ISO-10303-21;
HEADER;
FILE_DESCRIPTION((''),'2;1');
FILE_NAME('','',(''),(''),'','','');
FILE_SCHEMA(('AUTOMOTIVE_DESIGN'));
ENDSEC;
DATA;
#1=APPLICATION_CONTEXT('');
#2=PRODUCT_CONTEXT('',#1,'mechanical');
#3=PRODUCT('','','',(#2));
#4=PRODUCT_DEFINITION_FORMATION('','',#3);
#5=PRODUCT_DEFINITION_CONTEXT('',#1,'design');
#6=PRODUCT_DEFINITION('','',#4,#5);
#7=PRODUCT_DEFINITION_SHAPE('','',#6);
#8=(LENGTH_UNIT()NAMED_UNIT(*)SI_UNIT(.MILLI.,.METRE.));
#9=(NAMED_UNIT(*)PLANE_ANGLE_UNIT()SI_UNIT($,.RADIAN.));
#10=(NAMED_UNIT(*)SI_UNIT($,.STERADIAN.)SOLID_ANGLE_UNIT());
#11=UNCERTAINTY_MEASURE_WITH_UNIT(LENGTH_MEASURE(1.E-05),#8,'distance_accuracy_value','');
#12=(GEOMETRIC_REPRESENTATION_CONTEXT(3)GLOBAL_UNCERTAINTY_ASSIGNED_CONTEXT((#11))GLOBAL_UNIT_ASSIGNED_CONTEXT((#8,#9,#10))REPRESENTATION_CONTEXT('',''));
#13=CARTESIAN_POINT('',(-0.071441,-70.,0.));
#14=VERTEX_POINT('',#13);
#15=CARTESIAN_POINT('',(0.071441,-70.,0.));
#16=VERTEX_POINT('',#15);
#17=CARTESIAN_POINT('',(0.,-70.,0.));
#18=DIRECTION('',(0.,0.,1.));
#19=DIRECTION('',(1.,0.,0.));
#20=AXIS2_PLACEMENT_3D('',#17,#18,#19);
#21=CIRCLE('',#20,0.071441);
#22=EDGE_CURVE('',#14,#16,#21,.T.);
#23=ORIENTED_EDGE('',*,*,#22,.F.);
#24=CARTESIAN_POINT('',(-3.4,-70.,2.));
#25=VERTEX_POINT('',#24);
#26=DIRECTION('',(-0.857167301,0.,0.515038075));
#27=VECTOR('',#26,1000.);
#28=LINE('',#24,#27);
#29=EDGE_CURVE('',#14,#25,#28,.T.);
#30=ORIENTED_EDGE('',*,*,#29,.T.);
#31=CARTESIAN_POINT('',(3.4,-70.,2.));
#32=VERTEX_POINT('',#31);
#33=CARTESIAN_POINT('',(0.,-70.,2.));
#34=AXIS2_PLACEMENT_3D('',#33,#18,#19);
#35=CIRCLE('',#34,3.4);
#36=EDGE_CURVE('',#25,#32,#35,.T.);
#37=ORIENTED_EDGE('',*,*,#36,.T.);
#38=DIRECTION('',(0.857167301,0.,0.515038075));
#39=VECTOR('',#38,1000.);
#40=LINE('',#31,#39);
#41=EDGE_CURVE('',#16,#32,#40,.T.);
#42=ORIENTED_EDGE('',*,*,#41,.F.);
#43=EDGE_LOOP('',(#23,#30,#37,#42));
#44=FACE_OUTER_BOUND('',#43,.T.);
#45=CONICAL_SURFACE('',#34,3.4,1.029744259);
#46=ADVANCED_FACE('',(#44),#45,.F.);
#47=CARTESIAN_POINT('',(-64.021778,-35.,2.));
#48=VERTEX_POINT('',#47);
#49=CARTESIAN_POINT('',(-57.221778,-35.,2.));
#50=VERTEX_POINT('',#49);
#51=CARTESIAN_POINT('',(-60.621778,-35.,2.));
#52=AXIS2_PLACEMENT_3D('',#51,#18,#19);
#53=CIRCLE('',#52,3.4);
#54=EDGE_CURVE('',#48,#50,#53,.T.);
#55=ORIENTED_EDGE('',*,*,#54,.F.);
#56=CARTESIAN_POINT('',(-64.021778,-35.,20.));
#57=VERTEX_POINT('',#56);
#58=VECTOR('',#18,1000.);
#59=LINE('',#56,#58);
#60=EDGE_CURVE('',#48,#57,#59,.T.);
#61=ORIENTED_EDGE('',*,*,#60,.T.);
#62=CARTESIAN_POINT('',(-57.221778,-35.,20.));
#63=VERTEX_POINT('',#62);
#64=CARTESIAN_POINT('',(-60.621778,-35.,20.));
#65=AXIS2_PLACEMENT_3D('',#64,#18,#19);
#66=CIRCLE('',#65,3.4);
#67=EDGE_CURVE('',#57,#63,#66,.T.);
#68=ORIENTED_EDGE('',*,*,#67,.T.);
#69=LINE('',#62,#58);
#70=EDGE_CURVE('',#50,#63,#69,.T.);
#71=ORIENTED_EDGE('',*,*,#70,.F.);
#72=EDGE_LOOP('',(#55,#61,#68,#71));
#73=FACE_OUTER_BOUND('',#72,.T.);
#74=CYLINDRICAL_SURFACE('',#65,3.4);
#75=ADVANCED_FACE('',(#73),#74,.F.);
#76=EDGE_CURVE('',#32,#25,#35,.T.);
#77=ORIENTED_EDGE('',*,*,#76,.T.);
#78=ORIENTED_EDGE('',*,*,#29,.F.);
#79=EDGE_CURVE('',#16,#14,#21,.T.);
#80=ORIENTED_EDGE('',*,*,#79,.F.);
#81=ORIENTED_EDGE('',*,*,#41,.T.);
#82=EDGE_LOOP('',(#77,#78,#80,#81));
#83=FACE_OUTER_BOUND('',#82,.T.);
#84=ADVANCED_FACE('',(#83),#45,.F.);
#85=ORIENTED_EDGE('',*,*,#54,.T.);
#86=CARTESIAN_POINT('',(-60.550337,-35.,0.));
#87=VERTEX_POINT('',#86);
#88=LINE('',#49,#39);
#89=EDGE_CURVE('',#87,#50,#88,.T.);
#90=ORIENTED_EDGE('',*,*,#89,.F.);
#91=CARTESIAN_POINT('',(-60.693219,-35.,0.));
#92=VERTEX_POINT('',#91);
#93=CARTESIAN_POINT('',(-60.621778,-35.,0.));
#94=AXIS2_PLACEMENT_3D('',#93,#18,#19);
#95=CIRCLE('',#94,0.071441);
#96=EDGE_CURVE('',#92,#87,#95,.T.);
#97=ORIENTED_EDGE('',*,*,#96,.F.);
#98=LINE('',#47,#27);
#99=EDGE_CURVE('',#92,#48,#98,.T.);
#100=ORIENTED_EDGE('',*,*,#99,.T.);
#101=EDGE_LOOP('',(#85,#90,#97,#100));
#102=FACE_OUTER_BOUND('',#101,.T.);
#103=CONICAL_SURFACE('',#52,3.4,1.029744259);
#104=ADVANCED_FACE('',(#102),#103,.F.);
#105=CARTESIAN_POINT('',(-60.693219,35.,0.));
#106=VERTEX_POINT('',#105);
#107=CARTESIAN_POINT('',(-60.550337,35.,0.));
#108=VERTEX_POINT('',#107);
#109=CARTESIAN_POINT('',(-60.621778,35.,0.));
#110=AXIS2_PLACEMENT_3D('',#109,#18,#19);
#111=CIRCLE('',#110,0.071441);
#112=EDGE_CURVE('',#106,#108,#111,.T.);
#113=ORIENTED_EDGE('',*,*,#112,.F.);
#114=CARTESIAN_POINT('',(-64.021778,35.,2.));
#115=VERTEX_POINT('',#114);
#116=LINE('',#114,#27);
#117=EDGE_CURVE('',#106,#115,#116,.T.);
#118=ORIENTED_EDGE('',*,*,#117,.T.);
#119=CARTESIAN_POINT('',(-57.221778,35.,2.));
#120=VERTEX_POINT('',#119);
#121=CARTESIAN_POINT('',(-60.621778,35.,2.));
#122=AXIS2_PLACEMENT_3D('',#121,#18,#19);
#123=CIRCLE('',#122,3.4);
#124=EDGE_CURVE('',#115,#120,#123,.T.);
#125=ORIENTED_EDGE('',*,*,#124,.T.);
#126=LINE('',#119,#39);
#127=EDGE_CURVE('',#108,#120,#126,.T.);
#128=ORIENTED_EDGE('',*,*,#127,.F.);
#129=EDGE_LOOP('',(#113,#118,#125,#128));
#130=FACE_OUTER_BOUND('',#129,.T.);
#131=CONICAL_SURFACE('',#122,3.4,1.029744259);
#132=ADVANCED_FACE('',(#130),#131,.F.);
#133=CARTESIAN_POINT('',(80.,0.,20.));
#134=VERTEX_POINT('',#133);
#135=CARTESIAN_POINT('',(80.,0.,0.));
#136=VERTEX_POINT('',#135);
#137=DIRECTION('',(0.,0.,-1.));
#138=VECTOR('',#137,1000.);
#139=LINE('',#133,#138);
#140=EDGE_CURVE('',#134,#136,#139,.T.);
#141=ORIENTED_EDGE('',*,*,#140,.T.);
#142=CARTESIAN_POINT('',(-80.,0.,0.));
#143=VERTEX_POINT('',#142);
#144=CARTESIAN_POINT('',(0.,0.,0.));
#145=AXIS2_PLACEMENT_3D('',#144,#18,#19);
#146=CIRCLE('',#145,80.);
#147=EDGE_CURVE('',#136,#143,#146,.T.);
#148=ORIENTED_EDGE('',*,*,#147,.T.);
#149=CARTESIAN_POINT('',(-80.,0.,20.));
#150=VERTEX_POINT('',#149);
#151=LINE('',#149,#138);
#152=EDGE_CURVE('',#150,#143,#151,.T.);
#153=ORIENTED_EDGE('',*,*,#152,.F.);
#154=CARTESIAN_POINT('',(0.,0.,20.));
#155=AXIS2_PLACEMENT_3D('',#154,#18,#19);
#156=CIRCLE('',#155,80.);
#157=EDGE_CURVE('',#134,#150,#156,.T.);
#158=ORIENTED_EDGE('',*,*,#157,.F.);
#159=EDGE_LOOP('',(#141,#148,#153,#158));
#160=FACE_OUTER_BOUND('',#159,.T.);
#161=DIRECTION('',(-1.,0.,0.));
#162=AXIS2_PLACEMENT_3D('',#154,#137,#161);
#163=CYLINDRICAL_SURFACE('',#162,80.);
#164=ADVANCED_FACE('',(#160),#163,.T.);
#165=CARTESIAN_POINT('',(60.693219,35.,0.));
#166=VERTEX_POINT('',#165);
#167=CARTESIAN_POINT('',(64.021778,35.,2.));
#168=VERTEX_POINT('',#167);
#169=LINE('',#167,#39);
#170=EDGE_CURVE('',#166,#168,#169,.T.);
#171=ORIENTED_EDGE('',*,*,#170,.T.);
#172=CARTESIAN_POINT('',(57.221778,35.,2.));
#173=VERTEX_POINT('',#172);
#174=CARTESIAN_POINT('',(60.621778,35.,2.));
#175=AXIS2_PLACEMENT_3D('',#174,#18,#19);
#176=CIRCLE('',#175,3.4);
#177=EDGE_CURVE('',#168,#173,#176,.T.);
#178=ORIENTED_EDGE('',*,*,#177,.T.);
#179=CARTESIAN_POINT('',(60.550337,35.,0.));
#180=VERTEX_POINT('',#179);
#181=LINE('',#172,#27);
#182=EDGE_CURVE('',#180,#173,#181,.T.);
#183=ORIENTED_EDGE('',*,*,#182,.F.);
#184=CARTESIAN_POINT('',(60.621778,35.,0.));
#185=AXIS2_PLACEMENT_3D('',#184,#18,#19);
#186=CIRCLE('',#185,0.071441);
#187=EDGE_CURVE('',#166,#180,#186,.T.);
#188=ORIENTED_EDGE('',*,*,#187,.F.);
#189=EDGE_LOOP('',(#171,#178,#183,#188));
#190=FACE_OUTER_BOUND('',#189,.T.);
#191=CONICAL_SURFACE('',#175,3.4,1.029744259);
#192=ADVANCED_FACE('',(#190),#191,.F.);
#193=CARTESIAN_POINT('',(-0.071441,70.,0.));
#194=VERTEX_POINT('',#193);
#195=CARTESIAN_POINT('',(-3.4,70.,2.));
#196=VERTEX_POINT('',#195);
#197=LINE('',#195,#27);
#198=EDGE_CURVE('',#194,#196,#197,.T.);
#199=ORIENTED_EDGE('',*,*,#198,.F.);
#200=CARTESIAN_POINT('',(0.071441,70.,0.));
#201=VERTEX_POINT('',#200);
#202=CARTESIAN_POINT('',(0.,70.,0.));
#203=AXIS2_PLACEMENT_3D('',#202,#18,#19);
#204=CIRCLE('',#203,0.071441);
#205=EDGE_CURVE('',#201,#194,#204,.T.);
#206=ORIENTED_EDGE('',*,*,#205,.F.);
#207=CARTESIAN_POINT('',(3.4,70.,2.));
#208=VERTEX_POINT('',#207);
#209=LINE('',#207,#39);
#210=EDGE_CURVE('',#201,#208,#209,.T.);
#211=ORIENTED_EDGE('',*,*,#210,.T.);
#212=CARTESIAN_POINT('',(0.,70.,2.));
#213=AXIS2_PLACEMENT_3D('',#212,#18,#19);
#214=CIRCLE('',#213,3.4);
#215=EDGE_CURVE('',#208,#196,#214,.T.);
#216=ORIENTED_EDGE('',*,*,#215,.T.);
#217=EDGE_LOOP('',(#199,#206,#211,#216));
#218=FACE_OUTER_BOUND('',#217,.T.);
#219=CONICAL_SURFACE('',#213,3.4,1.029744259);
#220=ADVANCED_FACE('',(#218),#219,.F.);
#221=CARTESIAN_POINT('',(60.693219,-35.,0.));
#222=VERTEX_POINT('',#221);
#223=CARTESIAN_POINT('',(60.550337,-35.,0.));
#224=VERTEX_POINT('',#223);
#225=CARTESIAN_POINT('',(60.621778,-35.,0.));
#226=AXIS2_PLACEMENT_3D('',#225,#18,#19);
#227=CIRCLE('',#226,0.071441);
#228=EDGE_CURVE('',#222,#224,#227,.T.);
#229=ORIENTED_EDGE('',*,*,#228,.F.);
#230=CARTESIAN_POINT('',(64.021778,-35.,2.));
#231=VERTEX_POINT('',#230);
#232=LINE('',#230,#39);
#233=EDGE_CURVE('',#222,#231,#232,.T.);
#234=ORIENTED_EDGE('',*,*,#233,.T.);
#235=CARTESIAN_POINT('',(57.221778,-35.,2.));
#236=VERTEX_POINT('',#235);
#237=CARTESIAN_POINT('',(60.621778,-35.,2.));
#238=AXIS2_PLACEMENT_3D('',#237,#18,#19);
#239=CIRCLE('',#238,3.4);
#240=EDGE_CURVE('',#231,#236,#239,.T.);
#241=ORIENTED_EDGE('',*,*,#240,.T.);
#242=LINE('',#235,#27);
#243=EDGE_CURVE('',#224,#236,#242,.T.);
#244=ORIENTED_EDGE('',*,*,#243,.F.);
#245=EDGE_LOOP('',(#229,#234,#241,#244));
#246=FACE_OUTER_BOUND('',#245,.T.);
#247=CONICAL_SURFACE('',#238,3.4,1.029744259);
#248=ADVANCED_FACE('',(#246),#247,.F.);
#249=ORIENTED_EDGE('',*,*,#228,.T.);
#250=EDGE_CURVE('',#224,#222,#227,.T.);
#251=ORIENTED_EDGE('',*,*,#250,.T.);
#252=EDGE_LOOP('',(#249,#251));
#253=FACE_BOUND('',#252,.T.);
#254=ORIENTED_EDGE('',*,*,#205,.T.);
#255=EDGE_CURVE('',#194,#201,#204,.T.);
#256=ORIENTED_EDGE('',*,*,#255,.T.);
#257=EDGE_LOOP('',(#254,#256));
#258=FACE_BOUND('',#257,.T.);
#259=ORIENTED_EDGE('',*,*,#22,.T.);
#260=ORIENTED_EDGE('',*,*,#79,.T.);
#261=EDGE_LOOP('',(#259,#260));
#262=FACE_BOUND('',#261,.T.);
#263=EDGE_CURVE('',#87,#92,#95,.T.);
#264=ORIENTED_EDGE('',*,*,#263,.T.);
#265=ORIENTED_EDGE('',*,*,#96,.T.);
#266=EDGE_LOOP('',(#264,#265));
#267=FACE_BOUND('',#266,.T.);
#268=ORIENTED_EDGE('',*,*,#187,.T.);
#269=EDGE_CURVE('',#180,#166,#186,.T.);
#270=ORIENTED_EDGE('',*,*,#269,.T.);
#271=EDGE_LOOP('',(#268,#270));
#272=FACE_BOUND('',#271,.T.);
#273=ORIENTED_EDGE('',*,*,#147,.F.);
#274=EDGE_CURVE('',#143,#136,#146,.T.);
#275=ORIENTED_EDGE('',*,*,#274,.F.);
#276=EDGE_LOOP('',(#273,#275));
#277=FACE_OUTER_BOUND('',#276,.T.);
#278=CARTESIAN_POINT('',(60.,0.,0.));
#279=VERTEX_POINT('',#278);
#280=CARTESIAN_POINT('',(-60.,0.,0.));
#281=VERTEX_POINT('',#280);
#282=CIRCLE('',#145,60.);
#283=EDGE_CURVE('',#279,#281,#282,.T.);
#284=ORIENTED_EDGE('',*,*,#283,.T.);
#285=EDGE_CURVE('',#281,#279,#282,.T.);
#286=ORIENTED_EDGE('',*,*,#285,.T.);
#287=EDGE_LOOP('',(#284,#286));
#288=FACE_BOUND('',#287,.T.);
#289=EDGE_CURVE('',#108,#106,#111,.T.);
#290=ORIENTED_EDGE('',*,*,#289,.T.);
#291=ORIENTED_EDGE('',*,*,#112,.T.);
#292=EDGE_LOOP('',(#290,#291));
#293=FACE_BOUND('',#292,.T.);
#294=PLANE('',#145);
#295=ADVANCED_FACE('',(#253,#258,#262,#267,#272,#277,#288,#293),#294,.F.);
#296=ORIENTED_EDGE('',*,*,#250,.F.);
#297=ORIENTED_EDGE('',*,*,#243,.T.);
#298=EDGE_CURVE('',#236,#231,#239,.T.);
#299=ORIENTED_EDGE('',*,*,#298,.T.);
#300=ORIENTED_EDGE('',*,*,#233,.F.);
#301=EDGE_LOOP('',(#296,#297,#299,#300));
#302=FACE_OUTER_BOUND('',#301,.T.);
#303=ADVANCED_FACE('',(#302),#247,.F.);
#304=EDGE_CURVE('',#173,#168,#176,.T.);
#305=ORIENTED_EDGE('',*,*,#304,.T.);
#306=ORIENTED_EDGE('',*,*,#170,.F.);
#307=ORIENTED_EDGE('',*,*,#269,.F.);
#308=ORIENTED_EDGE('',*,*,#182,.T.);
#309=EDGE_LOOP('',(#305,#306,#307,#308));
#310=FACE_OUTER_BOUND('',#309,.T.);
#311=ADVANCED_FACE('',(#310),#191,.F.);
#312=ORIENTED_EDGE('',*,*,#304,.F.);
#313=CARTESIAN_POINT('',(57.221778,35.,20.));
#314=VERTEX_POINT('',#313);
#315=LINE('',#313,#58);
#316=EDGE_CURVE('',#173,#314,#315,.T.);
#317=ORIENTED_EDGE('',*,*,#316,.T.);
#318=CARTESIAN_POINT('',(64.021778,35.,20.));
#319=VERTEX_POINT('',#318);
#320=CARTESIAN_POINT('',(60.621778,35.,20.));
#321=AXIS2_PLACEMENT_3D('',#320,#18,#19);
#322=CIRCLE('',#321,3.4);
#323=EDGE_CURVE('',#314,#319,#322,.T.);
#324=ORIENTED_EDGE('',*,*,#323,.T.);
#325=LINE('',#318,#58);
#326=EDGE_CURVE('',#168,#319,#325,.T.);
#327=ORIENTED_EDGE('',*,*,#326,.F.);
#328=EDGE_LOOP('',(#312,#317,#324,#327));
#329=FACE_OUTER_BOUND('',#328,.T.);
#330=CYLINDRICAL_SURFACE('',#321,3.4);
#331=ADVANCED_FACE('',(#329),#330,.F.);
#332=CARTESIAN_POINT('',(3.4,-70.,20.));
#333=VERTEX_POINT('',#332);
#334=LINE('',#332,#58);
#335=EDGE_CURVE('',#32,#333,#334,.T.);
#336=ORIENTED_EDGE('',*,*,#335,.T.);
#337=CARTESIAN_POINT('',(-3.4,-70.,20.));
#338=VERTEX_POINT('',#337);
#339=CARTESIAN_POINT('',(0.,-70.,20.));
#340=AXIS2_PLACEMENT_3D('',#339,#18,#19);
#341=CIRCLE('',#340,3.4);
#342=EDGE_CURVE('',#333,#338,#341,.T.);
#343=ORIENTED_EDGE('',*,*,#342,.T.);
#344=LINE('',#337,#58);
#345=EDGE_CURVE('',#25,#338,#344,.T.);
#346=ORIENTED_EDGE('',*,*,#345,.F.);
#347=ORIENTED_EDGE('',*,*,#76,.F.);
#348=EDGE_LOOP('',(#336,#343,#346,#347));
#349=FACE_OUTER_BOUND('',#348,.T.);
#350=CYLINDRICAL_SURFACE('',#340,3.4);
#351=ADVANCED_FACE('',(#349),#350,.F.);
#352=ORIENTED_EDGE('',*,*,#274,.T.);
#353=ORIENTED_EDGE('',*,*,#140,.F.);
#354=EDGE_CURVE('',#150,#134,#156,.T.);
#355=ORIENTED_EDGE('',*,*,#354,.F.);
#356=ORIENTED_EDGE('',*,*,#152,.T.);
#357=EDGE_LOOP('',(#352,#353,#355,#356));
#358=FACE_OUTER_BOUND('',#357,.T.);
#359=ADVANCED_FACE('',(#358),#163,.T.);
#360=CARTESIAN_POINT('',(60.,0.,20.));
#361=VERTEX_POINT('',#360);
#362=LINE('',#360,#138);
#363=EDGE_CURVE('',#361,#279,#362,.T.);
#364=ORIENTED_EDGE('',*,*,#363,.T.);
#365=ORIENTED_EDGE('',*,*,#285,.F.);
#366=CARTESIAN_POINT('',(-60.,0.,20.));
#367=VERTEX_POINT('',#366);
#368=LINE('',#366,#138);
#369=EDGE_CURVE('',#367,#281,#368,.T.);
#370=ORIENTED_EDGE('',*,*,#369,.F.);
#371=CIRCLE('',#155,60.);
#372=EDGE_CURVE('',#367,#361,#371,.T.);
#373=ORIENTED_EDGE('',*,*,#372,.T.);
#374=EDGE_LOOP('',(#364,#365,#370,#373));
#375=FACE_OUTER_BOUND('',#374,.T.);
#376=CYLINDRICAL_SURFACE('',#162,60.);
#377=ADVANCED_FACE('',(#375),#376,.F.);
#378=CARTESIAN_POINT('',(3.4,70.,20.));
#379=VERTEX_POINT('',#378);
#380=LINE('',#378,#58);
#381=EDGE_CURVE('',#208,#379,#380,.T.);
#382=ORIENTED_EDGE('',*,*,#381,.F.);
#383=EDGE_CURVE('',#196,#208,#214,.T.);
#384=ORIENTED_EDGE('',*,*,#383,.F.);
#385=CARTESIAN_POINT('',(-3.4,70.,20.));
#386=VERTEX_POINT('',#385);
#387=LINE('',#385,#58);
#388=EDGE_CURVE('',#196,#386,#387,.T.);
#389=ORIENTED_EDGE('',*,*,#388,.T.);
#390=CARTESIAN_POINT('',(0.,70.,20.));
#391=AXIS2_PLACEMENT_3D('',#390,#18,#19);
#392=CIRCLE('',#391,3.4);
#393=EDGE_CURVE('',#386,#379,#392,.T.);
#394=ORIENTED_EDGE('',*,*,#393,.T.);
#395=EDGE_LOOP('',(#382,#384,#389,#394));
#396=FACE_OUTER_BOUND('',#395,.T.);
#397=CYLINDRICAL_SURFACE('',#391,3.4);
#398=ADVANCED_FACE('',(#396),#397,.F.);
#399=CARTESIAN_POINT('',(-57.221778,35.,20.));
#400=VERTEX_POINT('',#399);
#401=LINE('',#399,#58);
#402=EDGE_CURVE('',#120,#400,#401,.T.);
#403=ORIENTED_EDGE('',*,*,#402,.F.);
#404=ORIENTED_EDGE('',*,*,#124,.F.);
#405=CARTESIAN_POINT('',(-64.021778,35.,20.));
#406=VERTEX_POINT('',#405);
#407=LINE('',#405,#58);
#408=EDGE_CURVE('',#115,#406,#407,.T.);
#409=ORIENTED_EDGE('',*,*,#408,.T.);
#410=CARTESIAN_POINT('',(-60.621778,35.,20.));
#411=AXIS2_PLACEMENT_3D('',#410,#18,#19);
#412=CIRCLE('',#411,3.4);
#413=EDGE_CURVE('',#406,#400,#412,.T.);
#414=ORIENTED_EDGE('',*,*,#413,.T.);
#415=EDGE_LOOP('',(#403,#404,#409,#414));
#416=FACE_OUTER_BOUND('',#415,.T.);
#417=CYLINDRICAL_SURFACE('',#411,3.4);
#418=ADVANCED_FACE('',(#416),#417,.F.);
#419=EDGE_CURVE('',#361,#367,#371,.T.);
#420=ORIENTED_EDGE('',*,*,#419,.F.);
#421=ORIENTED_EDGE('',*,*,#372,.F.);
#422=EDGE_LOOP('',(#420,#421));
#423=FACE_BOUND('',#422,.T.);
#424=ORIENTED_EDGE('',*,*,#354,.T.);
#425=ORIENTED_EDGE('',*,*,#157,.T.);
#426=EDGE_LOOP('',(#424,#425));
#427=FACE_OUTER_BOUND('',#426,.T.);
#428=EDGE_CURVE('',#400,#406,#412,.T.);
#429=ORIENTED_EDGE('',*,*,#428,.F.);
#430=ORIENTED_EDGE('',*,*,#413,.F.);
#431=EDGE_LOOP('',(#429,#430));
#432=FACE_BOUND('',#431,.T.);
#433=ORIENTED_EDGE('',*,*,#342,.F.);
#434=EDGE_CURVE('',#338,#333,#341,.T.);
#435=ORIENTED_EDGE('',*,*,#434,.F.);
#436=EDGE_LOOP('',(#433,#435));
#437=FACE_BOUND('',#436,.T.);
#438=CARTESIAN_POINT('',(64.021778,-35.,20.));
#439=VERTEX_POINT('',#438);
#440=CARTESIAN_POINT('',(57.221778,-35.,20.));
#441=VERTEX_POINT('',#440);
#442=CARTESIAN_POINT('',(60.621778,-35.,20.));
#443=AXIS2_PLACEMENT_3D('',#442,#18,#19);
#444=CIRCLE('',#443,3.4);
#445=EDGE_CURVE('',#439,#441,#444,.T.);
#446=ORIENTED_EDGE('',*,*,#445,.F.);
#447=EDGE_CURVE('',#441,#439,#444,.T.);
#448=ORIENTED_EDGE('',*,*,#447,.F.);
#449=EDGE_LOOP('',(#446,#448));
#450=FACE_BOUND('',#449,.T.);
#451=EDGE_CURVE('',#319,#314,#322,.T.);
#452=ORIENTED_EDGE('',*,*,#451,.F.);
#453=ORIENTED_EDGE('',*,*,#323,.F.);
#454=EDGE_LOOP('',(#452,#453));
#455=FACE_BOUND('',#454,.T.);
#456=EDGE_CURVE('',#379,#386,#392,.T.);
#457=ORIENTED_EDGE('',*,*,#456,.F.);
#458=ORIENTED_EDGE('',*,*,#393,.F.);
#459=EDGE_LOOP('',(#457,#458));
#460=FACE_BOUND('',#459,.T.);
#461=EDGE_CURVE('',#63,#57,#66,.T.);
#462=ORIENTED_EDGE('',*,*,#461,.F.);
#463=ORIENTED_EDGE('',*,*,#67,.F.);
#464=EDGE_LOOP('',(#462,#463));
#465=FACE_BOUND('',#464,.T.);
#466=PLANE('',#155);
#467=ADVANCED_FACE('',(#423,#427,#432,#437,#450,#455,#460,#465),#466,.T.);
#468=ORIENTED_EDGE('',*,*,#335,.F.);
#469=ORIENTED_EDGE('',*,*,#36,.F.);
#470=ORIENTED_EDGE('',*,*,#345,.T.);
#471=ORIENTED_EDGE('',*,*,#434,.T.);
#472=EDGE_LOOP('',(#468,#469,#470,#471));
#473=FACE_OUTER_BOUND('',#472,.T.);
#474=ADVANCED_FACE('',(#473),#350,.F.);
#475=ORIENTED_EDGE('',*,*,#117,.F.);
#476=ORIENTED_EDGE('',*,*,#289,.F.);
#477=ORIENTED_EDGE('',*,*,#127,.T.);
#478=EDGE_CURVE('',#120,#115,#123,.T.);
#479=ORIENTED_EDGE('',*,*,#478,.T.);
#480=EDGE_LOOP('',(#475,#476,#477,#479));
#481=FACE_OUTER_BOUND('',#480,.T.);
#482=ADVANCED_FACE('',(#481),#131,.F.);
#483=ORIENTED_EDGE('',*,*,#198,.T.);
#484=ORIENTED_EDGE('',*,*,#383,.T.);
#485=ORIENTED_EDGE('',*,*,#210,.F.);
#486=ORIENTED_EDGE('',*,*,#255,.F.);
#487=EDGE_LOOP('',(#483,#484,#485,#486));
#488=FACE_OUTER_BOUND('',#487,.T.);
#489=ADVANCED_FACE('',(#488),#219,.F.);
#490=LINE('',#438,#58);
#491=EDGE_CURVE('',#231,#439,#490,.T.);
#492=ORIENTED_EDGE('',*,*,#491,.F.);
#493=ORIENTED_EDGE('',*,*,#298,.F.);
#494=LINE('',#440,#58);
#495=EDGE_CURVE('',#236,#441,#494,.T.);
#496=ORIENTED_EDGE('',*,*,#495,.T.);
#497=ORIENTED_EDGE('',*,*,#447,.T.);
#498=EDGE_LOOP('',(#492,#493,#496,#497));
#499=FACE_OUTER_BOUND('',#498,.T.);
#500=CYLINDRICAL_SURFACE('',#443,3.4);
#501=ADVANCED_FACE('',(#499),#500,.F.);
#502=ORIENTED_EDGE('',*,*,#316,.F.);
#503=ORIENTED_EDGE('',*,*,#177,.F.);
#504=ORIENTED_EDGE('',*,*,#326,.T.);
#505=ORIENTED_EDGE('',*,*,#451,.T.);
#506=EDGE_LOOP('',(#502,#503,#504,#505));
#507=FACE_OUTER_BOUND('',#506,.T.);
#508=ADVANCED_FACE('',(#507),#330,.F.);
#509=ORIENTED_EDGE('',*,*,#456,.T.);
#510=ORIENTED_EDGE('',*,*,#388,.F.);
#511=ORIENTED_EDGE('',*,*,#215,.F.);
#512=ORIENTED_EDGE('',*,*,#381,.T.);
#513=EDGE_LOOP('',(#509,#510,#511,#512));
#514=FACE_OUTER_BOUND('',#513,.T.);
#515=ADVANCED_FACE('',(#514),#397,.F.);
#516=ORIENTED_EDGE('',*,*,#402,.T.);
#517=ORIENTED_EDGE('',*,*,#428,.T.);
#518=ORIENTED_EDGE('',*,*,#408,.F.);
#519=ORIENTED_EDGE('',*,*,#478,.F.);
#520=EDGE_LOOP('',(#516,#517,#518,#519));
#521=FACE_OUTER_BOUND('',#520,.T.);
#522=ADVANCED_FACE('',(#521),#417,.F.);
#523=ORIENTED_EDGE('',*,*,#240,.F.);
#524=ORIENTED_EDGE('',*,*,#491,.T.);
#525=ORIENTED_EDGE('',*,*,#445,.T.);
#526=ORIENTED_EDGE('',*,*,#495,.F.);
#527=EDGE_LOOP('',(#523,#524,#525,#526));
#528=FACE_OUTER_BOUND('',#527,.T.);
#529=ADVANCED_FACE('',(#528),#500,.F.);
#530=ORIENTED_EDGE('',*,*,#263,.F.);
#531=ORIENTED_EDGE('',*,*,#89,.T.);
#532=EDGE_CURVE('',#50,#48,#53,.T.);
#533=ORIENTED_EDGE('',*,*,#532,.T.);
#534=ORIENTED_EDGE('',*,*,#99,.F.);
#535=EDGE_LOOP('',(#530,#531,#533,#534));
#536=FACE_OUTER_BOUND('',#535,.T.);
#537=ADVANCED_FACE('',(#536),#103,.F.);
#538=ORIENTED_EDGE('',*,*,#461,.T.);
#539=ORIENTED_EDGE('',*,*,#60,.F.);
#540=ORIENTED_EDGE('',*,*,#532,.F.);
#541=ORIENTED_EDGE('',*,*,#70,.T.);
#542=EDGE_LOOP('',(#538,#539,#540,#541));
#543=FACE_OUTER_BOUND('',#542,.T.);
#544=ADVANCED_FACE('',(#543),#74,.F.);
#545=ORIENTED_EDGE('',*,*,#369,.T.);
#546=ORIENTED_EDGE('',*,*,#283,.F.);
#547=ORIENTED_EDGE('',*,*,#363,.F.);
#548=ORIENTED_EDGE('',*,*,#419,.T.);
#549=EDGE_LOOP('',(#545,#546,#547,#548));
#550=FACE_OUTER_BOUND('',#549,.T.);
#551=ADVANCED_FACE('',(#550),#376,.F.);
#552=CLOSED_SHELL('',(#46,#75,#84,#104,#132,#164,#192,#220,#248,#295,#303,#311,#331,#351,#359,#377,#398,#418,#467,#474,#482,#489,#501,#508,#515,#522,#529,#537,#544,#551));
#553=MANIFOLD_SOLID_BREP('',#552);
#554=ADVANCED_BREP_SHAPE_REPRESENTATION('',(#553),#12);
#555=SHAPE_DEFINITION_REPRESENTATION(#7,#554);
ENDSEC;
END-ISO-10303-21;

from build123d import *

# Parameters (mm, degrees)
SKETCH1_R             = 80
SKETCH1_R_2           = 60
BOSS_EXTRUDE1_DEPTH   = 20
M8_TAPPED_HOLE1_D     = 6.8
M8_TAPPED_HOLE1_DEPTH = 18
M8_TAPPED_HOLE1_TIP   = 2.042926105


with BuildPart() as part:
    # Sketch1 → Boss-Extrude1 (new body)
    with BuildSketch(Plane.XY):
        Circle(SKETCH1_R)
        Circle(SKETCH1_R_2, mode=Mode.SUBTRACT)
    extrude(amount=BOSS_EXTRUDE1_DEPTH)

    # M8 Tapped Hole1
    with Locations(Plane(origin=(0, 70, 20), x_dir=(1, 0, 0), z_dir=(0, 0, 1))):
        with Locations((0, 0), (60.621778265, -35), (60.621778265, -105), (0, -140), (-60.621778265, -105), (-60.621778265, -35)):
            Hole(M8_TAPPED_HOLE1_D / 2, depth=M8_TAPPED_HOLE1_DEPTH)
            with Locations((0, 0, -(M8_TAPPED_HOLE1_DEPTH + M8_TAPPED_HOLE1_TIP / 2))):  # 118° drill point
                Cone(0, M8_TAPPED_HOLE1_D / 2, M8_TAPPED_HOLE1_TIP, mode=Mode.SUBTRACT)


solid = part.part
